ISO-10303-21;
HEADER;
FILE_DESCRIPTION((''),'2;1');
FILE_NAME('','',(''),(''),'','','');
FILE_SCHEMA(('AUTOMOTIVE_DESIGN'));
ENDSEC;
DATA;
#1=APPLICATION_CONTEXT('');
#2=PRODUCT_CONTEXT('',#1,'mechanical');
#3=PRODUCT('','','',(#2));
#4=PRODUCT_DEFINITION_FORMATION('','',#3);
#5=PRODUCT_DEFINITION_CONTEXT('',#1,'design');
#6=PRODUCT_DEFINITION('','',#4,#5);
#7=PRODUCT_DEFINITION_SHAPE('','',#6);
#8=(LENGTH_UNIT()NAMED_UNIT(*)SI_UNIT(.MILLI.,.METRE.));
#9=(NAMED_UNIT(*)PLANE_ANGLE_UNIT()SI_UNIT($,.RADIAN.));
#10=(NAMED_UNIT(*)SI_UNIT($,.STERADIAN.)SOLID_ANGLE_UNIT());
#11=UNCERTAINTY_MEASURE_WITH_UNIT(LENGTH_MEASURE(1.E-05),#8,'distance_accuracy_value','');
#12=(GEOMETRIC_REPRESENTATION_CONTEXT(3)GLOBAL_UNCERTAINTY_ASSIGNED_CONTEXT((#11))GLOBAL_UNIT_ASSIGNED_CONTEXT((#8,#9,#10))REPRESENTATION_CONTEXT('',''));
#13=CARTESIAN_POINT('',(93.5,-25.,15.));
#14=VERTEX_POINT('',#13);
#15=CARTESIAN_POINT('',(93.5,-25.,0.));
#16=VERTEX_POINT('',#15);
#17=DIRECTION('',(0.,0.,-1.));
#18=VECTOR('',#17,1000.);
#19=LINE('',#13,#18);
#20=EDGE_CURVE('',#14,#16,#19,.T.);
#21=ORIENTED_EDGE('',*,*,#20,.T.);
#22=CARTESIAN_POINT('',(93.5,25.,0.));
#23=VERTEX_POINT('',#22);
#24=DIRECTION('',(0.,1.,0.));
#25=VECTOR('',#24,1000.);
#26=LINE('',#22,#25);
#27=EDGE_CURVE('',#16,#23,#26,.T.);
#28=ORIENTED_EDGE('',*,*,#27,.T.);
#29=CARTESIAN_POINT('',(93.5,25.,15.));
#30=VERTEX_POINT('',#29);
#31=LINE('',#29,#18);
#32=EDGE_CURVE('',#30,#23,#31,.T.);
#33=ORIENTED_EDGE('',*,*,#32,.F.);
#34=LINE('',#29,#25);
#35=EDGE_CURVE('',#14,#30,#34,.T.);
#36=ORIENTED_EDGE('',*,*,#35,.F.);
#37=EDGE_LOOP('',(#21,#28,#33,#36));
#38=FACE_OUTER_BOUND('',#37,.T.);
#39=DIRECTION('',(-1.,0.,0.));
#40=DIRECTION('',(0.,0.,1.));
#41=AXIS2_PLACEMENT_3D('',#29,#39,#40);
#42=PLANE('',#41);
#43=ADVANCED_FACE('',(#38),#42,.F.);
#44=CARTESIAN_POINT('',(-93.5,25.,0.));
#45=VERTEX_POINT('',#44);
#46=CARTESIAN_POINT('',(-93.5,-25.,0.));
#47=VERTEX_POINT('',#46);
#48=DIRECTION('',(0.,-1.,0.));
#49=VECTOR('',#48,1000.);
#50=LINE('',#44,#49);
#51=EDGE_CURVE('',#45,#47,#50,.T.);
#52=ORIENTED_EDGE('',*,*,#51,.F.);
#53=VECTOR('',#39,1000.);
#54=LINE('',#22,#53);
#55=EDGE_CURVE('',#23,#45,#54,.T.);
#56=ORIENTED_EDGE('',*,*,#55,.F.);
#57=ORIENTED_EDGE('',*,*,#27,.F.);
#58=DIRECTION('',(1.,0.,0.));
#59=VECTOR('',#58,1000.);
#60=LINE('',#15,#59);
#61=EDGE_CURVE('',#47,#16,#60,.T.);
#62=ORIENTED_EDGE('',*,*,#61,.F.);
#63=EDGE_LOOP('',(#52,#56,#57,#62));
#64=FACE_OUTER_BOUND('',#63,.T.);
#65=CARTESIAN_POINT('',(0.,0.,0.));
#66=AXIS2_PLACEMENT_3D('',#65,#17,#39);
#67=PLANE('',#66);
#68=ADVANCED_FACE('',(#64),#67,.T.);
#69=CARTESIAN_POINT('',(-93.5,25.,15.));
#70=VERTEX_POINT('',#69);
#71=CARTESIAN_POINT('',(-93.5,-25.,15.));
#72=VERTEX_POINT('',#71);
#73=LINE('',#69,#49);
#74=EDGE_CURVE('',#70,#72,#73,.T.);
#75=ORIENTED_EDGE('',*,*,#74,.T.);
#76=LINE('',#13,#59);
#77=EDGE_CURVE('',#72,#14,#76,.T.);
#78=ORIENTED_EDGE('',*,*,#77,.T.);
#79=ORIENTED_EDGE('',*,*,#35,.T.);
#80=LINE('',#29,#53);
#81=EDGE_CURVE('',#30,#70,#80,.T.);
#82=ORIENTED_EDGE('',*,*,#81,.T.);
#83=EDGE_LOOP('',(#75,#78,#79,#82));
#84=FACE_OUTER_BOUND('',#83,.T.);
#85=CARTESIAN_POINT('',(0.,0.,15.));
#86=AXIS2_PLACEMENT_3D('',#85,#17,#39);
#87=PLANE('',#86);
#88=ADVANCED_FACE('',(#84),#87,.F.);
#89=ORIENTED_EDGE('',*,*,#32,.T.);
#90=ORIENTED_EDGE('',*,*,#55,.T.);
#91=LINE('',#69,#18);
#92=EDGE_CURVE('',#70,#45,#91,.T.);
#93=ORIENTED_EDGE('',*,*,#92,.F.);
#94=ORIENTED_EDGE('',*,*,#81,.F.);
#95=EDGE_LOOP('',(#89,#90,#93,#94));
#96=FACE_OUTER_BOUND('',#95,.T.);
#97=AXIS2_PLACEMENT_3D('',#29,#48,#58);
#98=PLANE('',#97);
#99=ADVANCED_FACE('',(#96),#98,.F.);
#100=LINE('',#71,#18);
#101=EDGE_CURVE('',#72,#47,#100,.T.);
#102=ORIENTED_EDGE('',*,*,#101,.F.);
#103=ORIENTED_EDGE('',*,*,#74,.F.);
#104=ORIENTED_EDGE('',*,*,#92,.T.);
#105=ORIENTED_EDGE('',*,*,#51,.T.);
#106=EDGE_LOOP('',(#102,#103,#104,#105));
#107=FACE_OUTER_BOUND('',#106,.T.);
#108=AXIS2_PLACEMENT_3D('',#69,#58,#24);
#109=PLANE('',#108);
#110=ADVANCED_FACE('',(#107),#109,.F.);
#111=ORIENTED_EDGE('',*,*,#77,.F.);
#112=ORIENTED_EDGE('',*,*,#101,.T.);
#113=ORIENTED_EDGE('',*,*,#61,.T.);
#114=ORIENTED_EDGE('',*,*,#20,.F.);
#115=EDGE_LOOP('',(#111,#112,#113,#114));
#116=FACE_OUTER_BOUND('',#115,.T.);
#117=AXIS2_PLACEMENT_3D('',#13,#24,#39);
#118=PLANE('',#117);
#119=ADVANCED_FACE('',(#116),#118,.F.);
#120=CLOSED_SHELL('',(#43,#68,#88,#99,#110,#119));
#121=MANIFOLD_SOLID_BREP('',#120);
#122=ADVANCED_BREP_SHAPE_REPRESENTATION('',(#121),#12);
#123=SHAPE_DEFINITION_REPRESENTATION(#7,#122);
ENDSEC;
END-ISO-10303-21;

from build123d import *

# Parameters (mm, degrees)
SKETCH_1_W      = 187
SKETCH_1_H      = 50
EXTRUDE_1_DEPTH = 15


with BuildPart() as part:
    # 草图1 → 凸台-拉伸1 (new body)
    with BuildSketch(Plane.XY):
        Rectangle(SKETCH_1_W, SKETCH_1_H)
    extrude(amount=EXTRUDE_1_DEPTH)


solid = part.part
